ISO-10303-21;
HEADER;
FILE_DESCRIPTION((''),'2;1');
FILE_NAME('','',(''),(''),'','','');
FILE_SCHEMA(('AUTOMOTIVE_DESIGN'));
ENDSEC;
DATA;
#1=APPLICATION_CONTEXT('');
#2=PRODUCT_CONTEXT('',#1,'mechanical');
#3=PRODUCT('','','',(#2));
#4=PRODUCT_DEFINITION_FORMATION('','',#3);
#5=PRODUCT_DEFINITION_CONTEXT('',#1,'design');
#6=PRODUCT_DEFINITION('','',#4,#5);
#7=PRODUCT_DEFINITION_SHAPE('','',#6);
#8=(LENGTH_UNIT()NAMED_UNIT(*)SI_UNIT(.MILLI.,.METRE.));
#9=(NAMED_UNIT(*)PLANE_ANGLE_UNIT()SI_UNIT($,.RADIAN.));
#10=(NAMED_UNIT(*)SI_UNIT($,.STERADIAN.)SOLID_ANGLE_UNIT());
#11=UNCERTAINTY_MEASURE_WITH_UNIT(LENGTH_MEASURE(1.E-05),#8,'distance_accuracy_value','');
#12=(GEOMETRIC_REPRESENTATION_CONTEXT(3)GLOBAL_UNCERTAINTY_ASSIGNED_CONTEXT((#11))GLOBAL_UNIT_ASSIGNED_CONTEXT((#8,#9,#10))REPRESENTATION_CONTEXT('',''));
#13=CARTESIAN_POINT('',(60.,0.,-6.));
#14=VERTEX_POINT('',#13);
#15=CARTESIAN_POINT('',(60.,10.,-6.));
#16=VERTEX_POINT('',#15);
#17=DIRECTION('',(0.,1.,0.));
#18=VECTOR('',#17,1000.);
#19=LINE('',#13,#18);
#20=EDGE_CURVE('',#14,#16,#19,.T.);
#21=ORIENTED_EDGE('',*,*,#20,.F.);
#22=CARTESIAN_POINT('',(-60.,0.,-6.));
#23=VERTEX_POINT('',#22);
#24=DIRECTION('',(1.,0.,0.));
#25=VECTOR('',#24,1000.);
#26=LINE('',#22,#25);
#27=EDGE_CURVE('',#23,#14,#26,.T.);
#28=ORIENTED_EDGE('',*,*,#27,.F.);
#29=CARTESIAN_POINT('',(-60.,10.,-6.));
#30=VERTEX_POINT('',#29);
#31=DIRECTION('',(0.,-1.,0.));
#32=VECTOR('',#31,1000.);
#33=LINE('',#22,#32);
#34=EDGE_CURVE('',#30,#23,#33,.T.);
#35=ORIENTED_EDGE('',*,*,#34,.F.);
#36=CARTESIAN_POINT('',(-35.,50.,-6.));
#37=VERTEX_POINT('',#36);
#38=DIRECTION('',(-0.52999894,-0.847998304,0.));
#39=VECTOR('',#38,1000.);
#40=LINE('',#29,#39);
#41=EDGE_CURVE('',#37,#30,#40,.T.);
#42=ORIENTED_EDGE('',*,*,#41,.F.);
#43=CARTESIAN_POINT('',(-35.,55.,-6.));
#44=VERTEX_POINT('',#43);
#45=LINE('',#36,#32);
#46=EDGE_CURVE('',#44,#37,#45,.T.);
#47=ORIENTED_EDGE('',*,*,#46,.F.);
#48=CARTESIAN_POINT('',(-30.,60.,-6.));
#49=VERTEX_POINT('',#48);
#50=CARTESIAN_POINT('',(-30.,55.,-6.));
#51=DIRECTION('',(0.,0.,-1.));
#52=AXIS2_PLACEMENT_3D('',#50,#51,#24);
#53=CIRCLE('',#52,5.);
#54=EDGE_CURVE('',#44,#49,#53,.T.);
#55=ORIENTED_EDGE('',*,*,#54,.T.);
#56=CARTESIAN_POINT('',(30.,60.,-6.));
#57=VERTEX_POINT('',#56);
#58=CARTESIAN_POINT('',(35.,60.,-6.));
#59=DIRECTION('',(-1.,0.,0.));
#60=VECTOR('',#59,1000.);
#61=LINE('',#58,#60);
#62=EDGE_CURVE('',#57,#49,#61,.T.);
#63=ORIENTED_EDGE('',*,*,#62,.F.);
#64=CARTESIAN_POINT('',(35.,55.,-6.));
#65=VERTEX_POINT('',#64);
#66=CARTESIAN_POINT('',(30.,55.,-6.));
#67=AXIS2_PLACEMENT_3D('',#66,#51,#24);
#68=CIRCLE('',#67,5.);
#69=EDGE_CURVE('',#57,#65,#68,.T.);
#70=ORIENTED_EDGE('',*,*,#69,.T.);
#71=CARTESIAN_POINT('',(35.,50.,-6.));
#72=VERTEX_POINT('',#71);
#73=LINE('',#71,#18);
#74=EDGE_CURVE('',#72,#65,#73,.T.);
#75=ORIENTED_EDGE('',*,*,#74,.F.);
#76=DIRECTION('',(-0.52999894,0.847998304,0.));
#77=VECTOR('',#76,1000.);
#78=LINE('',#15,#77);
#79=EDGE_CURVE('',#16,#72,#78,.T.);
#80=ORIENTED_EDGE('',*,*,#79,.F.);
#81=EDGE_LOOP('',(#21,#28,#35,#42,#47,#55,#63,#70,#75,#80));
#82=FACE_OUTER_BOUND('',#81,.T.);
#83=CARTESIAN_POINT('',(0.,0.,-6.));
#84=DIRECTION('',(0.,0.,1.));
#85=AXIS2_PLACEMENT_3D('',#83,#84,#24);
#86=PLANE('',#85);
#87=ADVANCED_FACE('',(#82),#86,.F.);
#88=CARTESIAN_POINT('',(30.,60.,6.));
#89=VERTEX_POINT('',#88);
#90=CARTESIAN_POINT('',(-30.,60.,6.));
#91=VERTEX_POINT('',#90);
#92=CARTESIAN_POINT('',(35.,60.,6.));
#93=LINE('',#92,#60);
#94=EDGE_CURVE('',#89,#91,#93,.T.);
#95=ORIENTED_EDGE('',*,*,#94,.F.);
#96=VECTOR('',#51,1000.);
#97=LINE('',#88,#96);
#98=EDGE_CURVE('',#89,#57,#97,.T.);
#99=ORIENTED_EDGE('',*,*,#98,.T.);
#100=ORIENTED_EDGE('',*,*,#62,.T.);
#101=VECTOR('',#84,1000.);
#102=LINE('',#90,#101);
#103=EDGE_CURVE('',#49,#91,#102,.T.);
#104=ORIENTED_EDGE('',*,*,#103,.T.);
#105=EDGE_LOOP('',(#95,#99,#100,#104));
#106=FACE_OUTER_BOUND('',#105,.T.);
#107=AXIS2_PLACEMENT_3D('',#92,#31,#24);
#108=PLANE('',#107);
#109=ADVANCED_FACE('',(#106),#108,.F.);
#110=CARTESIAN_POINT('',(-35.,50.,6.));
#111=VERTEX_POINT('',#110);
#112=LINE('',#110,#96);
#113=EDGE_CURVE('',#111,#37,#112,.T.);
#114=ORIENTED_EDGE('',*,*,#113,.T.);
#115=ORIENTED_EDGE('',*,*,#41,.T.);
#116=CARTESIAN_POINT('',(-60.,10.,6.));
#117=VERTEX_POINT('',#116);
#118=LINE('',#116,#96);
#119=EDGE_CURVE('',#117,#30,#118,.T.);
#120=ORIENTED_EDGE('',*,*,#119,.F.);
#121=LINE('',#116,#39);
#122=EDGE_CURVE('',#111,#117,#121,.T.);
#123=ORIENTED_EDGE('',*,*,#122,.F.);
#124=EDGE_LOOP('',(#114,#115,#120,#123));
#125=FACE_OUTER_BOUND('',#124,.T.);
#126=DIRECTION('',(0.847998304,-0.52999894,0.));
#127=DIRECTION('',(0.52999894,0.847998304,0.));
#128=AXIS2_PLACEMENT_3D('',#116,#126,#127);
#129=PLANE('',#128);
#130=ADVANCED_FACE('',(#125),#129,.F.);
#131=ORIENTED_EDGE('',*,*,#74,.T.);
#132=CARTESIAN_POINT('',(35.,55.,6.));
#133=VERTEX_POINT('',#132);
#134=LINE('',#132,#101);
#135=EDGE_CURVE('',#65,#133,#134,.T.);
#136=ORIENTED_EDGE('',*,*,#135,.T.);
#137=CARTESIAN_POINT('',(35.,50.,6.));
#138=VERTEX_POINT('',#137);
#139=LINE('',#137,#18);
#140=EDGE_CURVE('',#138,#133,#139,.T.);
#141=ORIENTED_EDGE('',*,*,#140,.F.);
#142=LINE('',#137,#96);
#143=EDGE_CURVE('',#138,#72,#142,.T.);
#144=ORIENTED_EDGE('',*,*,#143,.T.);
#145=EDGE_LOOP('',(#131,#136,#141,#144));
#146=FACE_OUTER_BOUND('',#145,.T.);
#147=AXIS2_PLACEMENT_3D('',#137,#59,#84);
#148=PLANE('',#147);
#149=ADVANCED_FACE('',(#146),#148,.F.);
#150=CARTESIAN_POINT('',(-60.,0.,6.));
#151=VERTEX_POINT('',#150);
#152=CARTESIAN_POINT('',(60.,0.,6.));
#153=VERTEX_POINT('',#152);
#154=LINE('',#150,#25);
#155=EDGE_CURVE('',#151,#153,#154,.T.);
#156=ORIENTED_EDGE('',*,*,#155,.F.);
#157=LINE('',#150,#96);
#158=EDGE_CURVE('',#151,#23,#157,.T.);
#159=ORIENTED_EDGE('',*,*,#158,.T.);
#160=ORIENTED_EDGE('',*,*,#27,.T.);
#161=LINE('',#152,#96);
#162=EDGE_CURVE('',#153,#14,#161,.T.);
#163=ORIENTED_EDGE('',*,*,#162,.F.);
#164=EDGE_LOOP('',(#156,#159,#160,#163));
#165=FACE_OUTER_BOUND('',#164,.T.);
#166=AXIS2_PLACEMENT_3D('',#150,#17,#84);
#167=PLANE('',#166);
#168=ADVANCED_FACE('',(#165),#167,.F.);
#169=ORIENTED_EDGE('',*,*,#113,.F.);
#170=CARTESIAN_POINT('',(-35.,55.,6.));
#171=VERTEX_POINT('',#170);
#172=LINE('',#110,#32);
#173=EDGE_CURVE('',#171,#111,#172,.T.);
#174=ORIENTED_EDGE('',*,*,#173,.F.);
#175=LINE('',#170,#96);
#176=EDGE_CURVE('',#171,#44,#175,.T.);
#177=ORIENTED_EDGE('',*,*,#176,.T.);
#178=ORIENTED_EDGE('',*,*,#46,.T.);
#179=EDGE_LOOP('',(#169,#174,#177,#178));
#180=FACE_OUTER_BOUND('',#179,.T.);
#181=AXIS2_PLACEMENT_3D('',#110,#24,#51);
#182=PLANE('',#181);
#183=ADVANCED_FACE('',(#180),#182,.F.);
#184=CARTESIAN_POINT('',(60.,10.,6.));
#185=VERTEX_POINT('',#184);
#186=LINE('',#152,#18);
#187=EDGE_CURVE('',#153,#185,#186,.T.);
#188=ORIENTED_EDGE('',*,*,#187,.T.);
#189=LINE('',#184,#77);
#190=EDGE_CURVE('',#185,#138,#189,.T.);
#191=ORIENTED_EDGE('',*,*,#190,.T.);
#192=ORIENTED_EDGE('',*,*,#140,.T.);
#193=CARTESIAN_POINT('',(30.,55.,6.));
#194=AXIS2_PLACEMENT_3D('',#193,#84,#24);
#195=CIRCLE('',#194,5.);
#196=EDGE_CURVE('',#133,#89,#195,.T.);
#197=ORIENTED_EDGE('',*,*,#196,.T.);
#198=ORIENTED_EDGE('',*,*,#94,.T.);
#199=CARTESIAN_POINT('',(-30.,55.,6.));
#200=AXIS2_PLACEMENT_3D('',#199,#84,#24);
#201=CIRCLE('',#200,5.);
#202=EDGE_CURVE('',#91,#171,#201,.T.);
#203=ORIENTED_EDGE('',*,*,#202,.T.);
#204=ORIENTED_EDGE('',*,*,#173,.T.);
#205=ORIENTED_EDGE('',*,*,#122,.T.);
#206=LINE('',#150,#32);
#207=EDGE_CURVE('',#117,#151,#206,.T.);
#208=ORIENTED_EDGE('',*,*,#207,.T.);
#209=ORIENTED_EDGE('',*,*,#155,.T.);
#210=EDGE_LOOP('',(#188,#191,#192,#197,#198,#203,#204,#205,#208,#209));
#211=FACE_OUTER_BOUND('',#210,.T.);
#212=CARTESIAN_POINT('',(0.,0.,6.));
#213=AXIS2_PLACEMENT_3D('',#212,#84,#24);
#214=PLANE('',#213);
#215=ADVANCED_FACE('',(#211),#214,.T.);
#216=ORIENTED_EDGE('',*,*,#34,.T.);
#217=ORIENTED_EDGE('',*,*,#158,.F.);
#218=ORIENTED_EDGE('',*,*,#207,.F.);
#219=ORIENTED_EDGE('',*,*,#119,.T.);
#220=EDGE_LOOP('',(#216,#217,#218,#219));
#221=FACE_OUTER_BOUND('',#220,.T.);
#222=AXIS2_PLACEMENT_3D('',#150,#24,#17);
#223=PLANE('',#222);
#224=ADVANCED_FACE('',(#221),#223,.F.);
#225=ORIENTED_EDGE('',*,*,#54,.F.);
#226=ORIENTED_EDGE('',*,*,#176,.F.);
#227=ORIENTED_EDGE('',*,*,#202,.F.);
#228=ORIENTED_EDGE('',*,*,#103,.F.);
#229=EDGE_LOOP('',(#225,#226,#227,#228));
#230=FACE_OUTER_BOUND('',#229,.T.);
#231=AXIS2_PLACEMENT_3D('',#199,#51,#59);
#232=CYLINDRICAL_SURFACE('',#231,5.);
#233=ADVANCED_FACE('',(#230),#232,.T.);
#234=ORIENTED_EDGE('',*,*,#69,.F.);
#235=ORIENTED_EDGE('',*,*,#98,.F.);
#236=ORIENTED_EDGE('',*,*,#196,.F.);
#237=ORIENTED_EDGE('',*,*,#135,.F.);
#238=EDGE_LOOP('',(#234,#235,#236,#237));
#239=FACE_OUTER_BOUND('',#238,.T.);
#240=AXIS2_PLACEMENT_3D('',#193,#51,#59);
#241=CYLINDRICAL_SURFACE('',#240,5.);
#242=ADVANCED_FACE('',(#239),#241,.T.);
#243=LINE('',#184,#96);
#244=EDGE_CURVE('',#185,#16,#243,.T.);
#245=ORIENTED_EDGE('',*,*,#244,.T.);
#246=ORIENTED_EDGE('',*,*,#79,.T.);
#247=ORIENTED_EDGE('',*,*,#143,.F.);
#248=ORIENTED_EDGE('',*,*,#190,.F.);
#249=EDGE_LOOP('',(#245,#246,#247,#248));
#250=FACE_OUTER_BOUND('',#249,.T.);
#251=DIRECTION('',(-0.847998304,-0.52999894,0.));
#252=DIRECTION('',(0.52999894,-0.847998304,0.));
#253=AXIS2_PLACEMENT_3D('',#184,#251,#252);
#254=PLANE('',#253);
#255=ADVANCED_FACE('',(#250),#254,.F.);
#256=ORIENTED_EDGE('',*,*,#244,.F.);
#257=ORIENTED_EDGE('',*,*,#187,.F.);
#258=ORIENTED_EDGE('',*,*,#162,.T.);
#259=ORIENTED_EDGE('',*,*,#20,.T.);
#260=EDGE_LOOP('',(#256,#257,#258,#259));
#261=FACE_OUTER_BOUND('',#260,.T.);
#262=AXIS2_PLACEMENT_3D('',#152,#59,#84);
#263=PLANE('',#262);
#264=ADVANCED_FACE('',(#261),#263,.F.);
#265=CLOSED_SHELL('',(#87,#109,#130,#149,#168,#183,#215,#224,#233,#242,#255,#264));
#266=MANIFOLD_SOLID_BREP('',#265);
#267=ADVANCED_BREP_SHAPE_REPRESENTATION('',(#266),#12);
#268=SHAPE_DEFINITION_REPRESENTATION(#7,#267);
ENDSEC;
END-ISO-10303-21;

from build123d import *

# Parameters (mm, degrees)
BOSS_EXTRUDE1_DEPTH = 6
FILLET1_R           = 5


with BuildPart() as part:
    # Sketch1 → Boss-Extrude1 (new, symmetric)
    with BuildSketch(Plane.XY):
        Polygon((-60, 0), (60, 0), (60, 10), (35, 50), (35, 60), (-35, 60), (-35, 50), (-60, 10), align=None)
    extrude(amount=BOSS_EXTRUDE1_DEPTH, both=True)

    # Fillet1
    fillet1_edges = [part.edges().sort_by_distance(p)[0] for p in [
        (-35, 60, 0),
        (35, 60, 0),
    ]]
    fillet(fillet1_edges, radius=FILLET1_R)


solid = part.part
